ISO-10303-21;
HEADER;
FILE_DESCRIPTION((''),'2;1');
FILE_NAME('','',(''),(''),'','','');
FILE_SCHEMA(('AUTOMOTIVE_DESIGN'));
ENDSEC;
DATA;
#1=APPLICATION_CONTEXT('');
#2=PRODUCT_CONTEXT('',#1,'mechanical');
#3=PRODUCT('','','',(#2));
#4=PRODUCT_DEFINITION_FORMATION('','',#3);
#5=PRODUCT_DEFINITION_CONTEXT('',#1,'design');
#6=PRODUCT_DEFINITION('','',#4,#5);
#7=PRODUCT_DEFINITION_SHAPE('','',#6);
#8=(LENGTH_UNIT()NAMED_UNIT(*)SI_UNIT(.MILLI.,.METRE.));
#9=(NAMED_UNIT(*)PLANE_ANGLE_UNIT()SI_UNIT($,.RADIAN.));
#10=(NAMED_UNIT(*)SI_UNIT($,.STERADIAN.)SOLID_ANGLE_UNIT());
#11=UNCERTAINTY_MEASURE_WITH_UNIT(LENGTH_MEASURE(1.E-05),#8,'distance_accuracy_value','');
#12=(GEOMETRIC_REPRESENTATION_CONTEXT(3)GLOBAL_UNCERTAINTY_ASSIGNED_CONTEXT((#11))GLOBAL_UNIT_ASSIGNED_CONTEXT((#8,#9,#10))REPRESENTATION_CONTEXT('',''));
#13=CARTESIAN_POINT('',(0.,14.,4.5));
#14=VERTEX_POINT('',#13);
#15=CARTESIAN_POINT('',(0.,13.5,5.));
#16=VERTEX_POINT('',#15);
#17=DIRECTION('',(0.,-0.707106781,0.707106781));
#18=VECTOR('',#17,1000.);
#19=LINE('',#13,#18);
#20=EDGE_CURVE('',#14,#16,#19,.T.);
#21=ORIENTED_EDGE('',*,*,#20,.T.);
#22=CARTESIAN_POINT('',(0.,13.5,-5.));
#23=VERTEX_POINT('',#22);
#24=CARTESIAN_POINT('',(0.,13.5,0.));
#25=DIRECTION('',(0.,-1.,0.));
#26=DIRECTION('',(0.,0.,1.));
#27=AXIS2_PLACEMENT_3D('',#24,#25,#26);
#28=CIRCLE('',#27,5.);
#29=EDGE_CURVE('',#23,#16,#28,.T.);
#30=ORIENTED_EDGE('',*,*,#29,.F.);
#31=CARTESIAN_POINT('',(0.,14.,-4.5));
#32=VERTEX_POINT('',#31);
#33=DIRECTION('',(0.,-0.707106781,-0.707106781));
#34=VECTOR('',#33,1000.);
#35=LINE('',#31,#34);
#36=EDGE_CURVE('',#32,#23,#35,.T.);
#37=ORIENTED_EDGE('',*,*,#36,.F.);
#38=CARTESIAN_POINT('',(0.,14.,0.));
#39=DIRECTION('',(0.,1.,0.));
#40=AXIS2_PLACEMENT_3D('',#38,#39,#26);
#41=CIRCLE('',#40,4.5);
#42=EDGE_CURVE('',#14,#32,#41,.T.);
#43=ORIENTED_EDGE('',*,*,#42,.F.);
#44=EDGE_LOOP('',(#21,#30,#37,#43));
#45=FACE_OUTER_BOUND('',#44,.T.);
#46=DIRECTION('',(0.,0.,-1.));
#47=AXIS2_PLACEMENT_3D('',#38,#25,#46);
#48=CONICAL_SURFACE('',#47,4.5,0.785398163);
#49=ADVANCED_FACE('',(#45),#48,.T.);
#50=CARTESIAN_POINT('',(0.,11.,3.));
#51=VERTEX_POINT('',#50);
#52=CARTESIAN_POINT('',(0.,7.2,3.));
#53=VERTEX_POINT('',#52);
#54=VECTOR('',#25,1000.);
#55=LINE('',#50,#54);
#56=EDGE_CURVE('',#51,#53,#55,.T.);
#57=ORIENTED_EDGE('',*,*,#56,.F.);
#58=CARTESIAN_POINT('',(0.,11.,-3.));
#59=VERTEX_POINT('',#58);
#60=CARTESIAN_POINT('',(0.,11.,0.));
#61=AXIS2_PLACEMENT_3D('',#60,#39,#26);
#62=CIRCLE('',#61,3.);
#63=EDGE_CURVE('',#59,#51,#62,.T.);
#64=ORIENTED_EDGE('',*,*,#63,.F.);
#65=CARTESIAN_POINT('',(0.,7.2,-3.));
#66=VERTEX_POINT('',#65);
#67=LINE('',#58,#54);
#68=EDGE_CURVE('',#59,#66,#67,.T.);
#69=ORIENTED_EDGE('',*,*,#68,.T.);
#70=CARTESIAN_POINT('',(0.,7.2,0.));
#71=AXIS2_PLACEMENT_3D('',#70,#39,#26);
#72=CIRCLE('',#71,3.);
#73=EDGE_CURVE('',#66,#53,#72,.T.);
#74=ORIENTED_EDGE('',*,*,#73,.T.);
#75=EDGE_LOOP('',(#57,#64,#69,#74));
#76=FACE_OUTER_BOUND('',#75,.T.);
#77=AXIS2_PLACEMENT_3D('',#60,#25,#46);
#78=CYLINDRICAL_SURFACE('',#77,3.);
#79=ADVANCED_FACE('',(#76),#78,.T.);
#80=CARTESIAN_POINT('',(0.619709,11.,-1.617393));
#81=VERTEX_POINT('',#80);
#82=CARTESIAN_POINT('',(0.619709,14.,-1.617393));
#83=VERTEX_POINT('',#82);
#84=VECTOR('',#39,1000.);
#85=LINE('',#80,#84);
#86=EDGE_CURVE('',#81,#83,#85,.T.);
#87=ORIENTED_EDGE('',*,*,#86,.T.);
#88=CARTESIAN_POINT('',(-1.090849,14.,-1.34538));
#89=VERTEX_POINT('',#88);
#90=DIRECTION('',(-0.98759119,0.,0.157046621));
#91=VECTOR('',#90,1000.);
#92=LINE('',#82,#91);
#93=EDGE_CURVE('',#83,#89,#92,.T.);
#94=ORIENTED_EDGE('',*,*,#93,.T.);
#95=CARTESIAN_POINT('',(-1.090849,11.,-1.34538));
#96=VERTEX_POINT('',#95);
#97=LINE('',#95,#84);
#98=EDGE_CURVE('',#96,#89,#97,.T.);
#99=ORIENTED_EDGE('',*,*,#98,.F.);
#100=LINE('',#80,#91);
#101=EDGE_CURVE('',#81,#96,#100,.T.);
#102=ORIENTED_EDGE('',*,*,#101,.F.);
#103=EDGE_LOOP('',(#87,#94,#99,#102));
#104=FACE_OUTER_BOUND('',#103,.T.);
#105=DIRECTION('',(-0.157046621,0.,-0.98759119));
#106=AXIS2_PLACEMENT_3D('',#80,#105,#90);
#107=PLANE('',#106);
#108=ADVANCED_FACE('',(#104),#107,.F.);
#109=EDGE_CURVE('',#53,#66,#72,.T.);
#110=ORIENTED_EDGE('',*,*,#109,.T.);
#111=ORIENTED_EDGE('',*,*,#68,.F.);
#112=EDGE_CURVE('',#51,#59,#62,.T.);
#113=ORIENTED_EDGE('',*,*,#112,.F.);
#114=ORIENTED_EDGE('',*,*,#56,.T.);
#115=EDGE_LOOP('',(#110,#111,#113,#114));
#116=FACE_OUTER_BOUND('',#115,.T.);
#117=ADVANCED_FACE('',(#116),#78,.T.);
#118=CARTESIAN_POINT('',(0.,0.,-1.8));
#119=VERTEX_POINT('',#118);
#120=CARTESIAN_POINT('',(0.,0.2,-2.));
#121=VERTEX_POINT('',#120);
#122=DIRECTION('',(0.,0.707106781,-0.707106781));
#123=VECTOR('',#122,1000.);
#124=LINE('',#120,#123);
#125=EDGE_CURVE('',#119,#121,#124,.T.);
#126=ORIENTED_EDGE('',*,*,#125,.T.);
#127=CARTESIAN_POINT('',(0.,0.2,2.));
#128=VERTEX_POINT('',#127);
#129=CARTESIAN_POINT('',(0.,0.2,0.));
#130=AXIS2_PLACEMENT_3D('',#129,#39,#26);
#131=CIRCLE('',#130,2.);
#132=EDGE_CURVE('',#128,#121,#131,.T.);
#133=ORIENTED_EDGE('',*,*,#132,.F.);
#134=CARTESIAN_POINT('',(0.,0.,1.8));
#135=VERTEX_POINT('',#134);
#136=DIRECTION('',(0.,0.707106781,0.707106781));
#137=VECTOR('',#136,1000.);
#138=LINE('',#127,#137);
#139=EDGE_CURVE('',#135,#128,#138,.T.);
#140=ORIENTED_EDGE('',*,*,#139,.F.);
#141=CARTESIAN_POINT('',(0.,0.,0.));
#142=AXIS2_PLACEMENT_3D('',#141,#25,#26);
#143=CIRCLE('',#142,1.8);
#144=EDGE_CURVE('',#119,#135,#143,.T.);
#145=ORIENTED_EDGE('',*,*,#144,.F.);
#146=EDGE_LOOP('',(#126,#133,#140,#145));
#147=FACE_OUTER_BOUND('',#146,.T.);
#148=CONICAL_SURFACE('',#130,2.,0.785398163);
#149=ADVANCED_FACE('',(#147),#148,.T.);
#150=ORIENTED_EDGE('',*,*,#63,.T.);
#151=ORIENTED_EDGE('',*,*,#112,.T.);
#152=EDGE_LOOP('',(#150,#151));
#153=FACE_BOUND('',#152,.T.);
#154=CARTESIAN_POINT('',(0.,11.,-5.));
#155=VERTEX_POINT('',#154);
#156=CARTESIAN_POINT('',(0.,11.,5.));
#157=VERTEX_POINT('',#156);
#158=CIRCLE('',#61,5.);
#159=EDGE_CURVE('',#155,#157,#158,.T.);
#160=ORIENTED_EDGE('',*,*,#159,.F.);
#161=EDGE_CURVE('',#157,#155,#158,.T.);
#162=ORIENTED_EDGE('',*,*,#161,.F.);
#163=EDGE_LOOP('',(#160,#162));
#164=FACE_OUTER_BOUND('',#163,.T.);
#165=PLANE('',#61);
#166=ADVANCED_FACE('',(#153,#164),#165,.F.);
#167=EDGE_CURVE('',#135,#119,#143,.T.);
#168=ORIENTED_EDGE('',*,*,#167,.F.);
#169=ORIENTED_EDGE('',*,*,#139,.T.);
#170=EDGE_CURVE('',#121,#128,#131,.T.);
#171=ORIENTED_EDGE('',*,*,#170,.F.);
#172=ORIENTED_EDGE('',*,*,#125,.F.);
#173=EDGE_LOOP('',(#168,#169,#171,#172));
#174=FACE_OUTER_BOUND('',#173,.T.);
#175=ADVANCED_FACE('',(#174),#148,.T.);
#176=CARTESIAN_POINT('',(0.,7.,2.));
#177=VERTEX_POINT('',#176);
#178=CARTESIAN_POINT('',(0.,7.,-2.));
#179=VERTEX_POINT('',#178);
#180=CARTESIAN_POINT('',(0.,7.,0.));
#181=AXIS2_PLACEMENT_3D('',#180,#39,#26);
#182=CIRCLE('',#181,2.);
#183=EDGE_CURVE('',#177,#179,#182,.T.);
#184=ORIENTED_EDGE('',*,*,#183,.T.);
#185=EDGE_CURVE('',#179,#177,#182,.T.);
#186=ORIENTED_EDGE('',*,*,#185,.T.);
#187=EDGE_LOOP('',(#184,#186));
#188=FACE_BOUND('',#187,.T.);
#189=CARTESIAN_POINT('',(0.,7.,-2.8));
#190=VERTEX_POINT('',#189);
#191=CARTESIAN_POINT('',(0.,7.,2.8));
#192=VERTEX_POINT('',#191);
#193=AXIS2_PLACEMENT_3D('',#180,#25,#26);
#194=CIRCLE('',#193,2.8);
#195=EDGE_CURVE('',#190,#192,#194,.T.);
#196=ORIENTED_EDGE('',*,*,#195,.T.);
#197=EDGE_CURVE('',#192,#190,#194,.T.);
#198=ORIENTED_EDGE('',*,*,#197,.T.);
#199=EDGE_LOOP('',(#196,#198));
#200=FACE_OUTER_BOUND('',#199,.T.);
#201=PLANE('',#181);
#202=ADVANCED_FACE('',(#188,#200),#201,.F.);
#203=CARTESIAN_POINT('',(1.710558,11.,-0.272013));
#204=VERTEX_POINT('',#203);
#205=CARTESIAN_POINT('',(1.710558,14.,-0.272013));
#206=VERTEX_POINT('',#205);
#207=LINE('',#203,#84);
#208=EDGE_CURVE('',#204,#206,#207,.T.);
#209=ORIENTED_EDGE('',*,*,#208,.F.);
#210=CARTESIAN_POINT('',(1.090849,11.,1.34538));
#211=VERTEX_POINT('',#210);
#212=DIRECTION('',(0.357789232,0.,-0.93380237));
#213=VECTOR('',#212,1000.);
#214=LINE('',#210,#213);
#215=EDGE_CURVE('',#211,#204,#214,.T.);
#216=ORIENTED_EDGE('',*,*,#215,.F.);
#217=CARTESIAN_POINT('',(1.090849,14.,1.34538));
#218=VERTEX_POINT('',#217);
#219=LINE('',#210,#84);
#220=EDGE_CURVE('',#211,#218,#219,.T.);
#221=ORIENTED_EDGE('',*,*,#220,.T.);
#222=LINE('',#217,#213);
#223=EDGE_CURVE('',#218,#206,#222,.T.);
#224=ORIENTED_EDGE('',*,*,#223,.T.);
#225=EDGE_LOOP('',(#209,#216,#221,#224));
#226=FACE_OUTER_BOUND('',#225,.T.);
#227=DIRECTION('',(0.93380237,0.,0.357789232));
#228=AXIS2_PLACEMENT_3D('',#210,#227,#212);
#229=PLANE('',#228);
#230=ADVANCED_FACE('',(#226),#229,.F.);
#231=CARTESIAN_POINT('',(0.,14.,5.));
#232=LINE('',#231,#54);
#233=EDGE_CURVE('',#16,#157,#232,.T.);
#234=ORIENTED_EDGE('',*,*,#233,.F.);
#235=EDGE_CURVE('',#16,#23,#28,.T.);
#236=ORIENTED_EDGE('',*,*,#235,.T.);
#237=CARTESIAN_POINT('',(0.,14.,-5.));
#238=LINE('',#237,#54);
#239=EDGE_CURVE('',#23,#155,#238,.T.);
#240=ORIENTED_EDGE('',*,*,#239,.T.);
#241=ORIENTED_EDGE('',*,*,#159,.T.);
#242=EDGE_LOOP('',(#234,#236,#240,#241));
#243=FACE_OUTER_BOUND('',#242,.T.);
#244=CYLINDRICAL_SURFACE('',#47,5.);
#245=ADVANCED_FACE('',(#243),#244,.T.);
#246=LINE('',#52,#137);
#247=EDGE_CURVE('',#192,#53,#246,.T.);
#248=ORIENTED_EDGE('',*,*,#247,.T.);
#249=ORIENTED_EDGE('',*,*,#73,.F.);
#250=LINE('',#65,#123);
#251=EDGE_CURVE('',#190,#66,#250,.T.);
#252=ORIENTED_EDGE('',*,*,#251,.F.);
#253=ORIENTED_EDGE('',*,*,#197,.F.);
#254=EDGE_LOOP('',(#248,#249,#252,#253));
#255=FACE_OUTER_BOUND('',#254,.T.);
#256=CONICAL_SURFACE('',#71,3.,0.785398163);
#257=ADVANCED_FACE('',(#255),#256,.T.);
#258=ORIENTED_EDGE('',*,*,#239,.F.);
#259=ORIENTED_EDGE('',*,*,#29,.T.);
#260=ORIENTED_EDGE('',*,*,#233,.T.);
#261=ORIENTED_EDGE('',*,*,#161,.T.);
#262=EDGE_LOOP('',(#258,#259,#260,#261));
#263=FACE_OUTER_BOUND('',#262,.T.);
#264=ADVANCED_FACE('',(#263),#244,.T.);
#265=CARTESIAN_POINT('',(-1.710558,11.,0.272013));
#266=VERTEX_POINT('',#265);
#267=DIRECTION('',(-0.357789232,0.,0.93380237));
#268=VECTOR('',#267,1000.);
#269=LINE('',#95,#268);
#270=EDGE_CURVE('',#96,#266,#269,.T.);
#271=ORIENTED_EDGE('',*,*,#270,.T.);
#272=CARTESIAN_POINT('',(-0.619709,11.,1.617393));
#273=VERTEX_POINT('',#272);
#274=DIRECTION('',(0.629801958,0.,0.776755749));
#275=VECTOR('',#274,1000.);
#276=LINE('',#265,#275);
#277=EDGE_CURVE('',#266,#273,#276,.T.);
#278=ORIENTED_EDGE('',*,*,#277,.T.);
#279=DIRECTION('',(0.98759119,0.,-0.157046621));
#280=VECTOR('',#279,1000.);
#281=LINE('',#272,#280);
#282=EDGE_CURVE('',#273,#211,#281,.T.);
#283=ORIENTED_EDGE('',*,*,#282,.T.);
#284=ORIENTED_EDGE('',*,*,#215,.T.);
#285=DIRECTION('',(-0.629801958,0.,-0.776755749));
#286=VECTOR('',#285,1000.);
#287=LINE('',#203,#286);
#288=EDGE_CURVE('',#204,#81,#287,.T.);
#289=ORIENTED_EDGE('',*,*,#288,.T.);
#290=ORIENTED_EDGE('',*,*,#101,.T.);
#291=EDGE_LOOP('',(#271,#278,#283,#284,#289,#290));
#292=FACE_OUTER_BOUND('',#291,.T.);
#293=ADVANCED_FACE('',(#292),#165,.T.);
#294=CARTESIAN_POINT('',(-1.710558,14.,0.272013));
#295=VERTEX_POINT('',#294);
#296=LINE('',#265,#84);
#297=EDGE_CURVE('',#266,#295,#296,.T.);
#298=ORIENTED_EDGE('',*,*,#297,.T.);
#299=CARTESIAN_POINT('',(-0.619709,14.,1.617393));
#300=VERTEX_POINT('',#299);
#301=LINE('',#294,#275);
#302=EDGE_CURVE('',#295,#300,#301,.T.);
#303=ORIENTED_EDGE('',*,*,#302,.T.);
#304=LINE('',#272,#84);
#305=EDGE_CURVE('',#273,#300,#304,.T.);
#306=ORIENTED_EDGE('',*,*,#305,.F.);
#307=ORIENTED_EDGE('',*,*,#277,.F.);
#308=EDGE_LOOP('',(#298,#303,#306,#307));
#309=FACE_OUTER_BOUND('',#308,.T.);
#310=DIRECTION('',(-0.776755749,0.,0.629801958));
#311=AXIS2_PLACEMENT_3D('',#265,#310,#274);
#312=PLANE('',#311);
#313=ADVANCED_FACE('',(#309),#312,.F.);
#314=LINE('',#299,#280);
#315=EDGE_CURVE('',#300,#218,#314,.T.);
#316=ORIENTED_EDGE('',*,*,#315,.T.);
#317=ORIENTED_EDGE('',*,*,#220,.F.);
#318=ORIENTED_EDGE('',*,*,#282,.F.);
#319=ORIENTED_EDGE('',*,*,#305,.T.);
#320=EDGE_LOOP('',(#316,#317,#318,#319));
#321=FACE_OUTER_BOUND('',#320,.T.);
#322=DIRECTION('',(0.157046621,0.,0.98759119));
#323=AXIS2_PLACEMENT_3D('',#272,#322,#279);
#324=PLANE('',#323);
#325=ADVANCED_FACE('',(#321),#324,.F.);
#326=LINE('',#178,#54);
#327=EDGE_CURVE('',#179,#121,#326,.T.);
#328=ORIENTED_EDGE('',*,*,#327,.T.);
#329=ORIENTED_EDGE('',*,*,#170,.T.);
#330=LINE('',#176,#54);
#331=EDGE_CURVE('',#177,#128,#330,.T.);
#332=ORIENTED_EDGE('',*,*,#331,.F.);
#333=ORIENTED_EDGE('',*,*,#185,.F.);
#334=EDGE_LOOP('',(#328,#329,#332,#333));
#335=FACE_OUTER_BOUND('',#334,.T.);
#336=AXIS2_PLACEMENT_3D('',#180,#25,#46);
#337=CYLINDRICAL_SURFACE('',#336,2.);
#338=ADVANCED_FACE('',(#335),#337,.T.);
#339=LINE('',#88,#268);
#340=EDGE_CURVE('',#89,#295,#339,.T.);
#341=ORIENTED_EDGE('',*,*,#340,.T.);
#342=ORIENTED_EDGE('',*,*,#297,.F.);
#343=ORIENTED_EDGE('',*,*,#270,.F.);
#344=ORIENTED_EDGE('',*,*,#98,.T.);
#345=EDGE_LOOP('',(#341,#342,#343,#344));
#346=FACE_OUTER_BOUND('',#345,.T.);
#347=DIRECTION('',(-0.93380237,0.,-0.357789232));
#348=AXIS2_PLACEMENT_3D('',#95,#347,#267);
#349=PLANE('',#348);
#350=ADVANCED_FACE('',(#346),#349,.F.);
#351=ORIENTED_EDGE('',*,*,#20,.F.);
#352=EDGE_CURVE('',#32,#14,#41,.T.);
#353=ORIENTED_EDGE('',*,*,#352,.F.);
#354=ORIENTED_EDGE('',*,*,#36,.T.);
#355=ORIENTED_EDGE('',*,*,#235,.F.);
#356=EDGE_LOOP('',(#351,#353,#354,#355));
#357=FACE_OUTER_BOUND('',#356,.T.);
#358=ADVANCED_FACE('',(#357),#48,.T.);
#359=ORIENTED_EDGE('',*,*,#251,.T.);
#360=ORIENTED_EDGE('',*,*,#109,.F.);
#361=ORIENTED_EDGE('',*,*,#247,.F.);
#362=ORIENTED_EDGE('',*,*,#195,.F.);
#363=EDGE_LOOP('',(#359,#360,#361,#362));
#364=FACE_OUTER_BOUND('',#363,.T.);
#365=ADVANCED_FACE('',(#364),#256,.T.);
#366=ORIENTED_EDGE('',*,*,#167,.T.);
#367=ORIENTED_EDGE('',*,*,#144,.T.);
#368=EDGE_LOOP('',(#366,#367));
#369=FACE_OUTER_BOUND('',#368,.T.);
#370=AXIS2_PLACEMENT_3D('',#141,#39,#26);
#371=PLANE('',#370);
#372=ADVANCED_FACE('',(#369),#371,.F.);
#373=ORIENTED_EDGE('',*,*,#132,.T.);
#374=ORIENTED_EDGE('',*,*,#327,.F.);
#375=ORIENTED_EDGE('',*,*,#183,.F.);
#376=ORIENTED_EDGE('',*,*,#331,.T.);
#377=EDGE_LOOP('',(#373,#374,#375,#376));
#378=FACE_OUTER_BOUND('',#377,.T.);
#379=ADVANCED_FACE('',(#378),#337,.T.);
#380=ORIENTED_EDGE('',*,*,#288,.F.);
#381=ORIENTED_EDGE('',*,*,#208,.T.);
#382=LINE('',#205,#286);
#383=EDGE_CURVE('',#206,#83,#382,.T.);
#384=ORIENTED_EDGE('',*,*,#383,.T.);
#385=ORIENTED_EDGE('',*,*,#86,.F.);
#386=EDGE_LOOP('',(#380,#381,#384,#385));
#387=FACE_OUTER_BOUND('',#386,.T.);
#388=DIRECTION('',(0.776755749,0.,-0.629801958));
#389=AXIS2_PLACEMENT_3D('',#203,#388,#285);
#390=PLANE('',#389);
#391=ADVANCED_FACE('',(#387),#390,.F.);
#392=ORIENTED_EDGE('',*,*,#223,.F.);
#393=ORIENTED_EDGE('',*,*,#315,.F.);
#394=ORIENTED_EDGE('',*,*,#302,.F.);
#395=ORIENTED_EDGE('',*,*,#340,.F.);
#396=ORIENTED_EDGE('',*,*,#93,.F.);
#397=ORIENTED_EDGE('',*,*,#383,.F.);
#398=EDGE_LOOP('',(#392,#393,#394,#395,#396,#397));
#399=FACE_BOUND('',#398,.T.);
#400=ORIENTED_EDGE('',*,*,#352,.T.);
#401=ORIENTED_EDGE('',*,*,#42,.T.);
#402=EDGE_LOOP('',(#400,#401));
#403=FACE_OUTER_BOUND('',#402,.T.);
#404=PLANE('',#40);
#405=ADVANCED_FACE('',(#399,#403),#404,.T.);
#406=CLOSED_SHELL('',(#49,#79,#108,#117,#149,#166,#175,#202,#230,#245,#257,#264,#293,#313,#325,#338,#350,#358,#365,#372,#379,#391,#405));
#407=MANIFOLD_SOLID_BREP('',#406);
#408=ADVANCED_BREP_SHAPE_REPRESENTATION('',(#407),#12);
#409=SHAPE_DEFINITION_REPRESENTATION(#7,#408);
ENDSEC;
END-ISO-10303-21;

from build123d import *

# Parameters (mm, degrees)
SKETCH_1_R          = 2
EXTRUDE_1_DEPTH     = 7
SKETCH_2_R          = 3
EXTRUDE_2_DEPTH     = 4
SKETCH_3_R          = 5
EXTRUDE_3_DEPTH     = 3
CHAMFER_1_SIZE      = 0.5
CHAMFER_2_SIZE      = 0.2
CHAMFER_3_SIZE      = 0.2
CUT_EXTRUDE_1_DEPTH = 3


with BuildPart() as part:
    # 草图1 → 凸台-拉伸1 (new body)
    with BuildSketch(Plane(origin=(0, 0, 0), x_dir=(1, 0, 0), z_dir=(0, 1, 0))):
        with Locations(Location((0, 0, 0), (0, 0, 270))):
            Circle(SKETCH_1_R)
    extrude(amount=EXTRUDE_1_DEPTH)

    # 草图2 → 凸台-拉伸2 (add)
    with BuildSketch(Plane(origin=(0, 7, 0), x_dir=(1, 0, 0), z_dir=(0, 1, 0))):
        with Locations(Location((0, 0, 0), (0, 0, 270))):
            Circle(SKETCH_2_R)
    extrude(amount=EXTRUDE_2_DEPTH)

    # 草图3 → 凸台-拉伸3 (add)
    with BuildSketch(Plane(origin=(0, 11, 0), x_dir=(1, 0, 0), z_dir=(0, 1, 0))):
        with Locations(Location((0, 0, 0), (0, 0, 270))):
            Circle(SKETCH_3_R)
    extrude(amount=EXTRUDE_3_DEPTH)

    # 倒角1
    chamfer_1_edges = [part.edges().sort_by_distance(p)[0] for p in [
        (0, 14, -5),
    ]]
    chamfer(chamfer_1_edges, length=CHAMFER_1_SIZE)

    # 倒角2
    chamfer_2_edges = [part.edges().sort_by_distance(p)[0] for p in [
        (0, 7, -3),
    ]]
    chamfer(chamfer_2_edges, length=CHAMFER_2_SIZE)

    # 倒角3
    chamfer_3_edges = [part.edges().sort_by_distance(p)[0] for p in [
        (0, 0, -2),
    ]]
    chamfer(chamfer_3_edges, length=CHAMFER_3_SIZE)

    # 草图4 → 切除-拉伸1 (cut)
    with BuildSketch(Plane(origin=(0, 14, 0), x_dir=(1, 0, 0), z_dir=(0, 1, 0))):
        Polygon((1.090848991, -1.345380422), (1.710558118, 0.272012727), (0.619709128, 1.617393149), (-1.090848991, 1.345380422), (-1.710558118, -0.272012727), (-0.619709128, -1.617393149), align=None)
    extrude(amount=-CUT_EXTRUDE_1_DEPTH, mode=Mode.SUBTRACT)


solid = part.part
